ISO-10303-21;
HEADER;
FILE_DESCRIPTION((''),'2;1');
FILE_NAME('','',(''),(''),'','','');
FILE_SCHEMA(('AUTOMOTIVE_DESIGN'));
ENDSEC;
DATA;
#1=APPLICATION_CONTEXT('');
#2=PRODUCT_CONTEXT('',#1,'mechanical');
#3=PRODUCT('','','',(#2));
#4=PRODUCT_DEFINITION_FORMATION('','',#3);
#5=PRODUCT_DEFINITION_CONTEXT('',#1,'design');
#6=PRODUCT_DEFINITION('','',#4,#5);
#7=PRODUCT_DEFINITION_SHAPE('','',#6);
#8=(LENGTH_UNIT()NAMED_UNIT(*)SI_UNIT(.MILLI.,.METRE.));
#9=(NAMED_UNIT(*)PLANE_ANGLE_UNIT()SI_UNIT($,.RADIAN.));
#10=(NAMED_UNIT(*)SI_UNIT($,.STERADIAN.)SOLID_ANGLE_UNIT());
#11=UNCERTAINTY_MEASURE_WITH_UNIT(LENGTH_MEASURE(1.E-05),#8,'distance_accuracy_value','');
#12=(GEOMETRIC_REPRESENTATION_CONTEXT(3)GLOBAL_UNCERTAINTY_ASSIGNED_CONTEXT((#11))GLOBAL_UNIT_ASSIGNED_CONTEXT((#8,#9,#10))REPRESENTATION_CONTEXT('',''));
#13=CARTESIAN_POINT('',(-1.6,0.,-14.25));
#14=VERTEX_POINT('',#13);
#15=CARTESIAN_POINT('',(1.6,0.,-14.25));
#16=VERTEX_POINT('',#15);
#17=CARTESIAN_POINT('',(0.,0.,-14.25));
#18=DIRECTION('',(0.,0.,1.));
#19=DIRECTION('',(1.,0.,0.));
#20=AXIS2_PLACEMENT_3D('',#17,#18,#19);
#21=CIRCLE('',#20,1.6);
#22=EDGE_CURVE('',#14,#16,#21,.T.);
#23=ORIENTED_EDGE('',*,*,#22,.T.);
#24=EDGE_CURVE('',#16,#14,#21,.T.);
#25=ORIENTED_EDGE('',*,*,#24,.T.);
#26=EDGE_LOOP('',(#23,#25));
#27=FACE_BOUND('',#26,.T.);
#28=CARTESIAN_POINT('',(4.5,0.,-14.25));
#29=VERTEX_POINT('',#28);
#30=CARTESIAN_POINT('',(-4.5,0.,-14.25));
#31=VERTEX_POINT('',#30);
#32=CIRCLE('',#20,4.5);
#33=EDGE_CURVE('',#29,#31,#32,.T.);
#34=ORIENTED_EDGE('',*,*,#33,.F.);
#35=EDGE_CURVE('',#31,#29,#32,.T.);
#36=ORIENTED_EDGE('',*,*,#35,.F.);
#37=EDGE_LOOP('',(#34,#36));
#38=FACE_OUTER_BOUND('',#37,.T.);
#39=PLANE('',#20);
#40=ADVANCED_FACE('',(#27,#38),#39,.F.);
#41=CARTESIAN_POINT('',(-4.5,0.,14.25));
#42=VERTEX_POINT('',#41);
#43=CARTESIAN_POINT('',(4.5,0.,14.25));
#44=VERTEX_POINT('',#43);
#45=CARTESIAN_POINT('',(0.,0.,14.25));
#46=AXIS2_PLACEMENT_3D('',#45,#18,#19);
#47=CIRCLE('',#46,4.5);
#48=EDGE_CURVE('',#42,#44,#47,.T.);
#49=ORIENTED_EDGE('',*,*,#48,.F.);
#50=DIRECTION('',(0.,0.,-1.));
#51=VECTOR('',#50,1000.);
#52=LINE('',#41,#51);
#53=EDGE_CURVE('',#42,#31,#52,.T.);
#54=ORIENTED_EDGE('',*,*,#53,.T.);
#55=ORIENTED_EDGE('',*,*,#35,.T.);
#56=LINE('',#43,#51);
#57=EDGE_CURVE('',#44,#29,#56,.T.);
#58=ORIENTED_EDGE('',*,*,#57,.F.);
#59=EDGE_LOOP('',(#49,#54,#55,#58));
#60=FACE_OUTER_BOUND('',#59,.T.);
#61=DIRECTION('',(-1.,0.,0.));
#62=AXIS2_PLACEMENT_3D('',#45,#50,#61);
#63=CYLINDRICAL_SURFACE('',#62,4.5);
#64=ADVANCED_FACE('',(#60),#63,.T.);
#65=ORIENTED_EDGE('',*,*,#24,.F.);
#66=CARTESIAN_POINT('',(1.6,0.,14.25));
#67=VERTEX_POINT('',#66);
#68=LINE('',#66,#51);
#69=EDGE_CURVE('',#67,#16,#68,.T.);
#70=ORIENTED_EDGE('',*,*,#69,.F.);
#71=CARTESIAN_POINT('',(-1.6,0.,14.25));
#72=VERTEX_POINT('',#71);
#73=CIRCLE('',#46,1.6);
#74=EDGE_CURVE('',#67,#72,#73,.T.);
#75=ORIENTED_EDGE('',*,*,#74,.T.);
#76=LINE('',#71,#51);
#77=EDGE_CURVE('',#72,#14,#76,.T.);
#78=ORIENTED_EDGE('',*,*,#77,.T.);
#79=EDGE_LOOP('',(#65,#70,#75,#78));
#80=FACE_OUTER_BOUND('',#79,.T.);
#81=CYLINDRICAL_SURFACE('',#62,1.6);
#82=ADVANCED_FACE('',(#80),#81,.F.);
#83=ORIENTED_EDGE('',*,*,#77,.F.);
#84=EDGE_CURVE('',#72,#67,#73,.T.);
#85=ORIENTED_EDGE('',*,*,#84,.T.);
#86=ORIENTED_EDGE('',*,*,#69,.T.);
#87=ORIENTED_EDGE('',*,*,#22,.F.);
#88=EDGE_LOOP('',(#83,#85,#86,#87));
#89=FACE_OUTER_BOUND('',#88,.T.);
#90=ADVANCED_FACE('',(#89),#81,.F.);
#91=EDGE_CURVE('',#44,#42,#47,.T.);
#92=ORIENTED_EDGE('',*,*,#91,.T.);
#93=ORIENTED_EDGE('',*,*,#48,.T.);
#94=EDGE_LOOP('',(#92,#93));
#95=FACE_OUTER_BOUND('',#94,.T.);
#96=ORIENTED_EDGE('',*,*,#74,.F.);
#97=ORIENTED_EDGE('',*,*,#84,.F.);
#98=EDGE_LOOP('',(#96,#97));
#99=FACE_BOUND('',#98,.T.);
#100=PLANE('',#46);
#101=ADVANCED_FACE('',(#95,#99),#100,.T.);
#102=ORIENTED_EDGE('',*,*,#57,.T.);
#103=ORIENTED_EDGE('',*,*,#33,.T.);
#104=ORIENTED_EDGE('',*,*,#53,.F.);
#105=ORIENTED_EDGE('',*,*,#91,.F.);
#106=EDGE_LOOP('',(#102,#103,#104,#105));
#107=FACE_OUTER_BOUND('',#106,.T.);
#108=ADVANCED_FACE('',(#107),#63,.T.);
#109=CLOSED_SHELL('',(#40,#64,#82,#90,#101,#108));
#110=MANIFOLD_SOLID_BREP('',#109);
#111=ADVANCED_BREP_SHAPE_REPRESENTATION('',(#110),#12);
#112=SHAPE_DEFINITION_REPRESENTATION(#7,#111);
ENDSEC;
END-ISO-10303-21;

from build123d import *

# Parameters (mm, degrees)
SKETCH_1_R      = 4.5
SKETCH_1_R_2    = 1.6
EXTRUDE_1_DEPTH = 14.25


with BuildPart() as part:
    # 草图1 → 凸台-拉伸1 (new, symmetric)
    with BuildSketch(Plane.XY):
        with Locations(Location((0, 0, 0), (0, 0, 180))):
            Circle(SKETCH_1_R)
        with Locations(Location((0, 0, 0), (0, 0, 180))):
            Circle(SKETCH_1_R_2, mode=Mode.SUBTRACT)
    extrude(amount=EXTRUDE_1_DEPTH, both=True)


solid = part.part
